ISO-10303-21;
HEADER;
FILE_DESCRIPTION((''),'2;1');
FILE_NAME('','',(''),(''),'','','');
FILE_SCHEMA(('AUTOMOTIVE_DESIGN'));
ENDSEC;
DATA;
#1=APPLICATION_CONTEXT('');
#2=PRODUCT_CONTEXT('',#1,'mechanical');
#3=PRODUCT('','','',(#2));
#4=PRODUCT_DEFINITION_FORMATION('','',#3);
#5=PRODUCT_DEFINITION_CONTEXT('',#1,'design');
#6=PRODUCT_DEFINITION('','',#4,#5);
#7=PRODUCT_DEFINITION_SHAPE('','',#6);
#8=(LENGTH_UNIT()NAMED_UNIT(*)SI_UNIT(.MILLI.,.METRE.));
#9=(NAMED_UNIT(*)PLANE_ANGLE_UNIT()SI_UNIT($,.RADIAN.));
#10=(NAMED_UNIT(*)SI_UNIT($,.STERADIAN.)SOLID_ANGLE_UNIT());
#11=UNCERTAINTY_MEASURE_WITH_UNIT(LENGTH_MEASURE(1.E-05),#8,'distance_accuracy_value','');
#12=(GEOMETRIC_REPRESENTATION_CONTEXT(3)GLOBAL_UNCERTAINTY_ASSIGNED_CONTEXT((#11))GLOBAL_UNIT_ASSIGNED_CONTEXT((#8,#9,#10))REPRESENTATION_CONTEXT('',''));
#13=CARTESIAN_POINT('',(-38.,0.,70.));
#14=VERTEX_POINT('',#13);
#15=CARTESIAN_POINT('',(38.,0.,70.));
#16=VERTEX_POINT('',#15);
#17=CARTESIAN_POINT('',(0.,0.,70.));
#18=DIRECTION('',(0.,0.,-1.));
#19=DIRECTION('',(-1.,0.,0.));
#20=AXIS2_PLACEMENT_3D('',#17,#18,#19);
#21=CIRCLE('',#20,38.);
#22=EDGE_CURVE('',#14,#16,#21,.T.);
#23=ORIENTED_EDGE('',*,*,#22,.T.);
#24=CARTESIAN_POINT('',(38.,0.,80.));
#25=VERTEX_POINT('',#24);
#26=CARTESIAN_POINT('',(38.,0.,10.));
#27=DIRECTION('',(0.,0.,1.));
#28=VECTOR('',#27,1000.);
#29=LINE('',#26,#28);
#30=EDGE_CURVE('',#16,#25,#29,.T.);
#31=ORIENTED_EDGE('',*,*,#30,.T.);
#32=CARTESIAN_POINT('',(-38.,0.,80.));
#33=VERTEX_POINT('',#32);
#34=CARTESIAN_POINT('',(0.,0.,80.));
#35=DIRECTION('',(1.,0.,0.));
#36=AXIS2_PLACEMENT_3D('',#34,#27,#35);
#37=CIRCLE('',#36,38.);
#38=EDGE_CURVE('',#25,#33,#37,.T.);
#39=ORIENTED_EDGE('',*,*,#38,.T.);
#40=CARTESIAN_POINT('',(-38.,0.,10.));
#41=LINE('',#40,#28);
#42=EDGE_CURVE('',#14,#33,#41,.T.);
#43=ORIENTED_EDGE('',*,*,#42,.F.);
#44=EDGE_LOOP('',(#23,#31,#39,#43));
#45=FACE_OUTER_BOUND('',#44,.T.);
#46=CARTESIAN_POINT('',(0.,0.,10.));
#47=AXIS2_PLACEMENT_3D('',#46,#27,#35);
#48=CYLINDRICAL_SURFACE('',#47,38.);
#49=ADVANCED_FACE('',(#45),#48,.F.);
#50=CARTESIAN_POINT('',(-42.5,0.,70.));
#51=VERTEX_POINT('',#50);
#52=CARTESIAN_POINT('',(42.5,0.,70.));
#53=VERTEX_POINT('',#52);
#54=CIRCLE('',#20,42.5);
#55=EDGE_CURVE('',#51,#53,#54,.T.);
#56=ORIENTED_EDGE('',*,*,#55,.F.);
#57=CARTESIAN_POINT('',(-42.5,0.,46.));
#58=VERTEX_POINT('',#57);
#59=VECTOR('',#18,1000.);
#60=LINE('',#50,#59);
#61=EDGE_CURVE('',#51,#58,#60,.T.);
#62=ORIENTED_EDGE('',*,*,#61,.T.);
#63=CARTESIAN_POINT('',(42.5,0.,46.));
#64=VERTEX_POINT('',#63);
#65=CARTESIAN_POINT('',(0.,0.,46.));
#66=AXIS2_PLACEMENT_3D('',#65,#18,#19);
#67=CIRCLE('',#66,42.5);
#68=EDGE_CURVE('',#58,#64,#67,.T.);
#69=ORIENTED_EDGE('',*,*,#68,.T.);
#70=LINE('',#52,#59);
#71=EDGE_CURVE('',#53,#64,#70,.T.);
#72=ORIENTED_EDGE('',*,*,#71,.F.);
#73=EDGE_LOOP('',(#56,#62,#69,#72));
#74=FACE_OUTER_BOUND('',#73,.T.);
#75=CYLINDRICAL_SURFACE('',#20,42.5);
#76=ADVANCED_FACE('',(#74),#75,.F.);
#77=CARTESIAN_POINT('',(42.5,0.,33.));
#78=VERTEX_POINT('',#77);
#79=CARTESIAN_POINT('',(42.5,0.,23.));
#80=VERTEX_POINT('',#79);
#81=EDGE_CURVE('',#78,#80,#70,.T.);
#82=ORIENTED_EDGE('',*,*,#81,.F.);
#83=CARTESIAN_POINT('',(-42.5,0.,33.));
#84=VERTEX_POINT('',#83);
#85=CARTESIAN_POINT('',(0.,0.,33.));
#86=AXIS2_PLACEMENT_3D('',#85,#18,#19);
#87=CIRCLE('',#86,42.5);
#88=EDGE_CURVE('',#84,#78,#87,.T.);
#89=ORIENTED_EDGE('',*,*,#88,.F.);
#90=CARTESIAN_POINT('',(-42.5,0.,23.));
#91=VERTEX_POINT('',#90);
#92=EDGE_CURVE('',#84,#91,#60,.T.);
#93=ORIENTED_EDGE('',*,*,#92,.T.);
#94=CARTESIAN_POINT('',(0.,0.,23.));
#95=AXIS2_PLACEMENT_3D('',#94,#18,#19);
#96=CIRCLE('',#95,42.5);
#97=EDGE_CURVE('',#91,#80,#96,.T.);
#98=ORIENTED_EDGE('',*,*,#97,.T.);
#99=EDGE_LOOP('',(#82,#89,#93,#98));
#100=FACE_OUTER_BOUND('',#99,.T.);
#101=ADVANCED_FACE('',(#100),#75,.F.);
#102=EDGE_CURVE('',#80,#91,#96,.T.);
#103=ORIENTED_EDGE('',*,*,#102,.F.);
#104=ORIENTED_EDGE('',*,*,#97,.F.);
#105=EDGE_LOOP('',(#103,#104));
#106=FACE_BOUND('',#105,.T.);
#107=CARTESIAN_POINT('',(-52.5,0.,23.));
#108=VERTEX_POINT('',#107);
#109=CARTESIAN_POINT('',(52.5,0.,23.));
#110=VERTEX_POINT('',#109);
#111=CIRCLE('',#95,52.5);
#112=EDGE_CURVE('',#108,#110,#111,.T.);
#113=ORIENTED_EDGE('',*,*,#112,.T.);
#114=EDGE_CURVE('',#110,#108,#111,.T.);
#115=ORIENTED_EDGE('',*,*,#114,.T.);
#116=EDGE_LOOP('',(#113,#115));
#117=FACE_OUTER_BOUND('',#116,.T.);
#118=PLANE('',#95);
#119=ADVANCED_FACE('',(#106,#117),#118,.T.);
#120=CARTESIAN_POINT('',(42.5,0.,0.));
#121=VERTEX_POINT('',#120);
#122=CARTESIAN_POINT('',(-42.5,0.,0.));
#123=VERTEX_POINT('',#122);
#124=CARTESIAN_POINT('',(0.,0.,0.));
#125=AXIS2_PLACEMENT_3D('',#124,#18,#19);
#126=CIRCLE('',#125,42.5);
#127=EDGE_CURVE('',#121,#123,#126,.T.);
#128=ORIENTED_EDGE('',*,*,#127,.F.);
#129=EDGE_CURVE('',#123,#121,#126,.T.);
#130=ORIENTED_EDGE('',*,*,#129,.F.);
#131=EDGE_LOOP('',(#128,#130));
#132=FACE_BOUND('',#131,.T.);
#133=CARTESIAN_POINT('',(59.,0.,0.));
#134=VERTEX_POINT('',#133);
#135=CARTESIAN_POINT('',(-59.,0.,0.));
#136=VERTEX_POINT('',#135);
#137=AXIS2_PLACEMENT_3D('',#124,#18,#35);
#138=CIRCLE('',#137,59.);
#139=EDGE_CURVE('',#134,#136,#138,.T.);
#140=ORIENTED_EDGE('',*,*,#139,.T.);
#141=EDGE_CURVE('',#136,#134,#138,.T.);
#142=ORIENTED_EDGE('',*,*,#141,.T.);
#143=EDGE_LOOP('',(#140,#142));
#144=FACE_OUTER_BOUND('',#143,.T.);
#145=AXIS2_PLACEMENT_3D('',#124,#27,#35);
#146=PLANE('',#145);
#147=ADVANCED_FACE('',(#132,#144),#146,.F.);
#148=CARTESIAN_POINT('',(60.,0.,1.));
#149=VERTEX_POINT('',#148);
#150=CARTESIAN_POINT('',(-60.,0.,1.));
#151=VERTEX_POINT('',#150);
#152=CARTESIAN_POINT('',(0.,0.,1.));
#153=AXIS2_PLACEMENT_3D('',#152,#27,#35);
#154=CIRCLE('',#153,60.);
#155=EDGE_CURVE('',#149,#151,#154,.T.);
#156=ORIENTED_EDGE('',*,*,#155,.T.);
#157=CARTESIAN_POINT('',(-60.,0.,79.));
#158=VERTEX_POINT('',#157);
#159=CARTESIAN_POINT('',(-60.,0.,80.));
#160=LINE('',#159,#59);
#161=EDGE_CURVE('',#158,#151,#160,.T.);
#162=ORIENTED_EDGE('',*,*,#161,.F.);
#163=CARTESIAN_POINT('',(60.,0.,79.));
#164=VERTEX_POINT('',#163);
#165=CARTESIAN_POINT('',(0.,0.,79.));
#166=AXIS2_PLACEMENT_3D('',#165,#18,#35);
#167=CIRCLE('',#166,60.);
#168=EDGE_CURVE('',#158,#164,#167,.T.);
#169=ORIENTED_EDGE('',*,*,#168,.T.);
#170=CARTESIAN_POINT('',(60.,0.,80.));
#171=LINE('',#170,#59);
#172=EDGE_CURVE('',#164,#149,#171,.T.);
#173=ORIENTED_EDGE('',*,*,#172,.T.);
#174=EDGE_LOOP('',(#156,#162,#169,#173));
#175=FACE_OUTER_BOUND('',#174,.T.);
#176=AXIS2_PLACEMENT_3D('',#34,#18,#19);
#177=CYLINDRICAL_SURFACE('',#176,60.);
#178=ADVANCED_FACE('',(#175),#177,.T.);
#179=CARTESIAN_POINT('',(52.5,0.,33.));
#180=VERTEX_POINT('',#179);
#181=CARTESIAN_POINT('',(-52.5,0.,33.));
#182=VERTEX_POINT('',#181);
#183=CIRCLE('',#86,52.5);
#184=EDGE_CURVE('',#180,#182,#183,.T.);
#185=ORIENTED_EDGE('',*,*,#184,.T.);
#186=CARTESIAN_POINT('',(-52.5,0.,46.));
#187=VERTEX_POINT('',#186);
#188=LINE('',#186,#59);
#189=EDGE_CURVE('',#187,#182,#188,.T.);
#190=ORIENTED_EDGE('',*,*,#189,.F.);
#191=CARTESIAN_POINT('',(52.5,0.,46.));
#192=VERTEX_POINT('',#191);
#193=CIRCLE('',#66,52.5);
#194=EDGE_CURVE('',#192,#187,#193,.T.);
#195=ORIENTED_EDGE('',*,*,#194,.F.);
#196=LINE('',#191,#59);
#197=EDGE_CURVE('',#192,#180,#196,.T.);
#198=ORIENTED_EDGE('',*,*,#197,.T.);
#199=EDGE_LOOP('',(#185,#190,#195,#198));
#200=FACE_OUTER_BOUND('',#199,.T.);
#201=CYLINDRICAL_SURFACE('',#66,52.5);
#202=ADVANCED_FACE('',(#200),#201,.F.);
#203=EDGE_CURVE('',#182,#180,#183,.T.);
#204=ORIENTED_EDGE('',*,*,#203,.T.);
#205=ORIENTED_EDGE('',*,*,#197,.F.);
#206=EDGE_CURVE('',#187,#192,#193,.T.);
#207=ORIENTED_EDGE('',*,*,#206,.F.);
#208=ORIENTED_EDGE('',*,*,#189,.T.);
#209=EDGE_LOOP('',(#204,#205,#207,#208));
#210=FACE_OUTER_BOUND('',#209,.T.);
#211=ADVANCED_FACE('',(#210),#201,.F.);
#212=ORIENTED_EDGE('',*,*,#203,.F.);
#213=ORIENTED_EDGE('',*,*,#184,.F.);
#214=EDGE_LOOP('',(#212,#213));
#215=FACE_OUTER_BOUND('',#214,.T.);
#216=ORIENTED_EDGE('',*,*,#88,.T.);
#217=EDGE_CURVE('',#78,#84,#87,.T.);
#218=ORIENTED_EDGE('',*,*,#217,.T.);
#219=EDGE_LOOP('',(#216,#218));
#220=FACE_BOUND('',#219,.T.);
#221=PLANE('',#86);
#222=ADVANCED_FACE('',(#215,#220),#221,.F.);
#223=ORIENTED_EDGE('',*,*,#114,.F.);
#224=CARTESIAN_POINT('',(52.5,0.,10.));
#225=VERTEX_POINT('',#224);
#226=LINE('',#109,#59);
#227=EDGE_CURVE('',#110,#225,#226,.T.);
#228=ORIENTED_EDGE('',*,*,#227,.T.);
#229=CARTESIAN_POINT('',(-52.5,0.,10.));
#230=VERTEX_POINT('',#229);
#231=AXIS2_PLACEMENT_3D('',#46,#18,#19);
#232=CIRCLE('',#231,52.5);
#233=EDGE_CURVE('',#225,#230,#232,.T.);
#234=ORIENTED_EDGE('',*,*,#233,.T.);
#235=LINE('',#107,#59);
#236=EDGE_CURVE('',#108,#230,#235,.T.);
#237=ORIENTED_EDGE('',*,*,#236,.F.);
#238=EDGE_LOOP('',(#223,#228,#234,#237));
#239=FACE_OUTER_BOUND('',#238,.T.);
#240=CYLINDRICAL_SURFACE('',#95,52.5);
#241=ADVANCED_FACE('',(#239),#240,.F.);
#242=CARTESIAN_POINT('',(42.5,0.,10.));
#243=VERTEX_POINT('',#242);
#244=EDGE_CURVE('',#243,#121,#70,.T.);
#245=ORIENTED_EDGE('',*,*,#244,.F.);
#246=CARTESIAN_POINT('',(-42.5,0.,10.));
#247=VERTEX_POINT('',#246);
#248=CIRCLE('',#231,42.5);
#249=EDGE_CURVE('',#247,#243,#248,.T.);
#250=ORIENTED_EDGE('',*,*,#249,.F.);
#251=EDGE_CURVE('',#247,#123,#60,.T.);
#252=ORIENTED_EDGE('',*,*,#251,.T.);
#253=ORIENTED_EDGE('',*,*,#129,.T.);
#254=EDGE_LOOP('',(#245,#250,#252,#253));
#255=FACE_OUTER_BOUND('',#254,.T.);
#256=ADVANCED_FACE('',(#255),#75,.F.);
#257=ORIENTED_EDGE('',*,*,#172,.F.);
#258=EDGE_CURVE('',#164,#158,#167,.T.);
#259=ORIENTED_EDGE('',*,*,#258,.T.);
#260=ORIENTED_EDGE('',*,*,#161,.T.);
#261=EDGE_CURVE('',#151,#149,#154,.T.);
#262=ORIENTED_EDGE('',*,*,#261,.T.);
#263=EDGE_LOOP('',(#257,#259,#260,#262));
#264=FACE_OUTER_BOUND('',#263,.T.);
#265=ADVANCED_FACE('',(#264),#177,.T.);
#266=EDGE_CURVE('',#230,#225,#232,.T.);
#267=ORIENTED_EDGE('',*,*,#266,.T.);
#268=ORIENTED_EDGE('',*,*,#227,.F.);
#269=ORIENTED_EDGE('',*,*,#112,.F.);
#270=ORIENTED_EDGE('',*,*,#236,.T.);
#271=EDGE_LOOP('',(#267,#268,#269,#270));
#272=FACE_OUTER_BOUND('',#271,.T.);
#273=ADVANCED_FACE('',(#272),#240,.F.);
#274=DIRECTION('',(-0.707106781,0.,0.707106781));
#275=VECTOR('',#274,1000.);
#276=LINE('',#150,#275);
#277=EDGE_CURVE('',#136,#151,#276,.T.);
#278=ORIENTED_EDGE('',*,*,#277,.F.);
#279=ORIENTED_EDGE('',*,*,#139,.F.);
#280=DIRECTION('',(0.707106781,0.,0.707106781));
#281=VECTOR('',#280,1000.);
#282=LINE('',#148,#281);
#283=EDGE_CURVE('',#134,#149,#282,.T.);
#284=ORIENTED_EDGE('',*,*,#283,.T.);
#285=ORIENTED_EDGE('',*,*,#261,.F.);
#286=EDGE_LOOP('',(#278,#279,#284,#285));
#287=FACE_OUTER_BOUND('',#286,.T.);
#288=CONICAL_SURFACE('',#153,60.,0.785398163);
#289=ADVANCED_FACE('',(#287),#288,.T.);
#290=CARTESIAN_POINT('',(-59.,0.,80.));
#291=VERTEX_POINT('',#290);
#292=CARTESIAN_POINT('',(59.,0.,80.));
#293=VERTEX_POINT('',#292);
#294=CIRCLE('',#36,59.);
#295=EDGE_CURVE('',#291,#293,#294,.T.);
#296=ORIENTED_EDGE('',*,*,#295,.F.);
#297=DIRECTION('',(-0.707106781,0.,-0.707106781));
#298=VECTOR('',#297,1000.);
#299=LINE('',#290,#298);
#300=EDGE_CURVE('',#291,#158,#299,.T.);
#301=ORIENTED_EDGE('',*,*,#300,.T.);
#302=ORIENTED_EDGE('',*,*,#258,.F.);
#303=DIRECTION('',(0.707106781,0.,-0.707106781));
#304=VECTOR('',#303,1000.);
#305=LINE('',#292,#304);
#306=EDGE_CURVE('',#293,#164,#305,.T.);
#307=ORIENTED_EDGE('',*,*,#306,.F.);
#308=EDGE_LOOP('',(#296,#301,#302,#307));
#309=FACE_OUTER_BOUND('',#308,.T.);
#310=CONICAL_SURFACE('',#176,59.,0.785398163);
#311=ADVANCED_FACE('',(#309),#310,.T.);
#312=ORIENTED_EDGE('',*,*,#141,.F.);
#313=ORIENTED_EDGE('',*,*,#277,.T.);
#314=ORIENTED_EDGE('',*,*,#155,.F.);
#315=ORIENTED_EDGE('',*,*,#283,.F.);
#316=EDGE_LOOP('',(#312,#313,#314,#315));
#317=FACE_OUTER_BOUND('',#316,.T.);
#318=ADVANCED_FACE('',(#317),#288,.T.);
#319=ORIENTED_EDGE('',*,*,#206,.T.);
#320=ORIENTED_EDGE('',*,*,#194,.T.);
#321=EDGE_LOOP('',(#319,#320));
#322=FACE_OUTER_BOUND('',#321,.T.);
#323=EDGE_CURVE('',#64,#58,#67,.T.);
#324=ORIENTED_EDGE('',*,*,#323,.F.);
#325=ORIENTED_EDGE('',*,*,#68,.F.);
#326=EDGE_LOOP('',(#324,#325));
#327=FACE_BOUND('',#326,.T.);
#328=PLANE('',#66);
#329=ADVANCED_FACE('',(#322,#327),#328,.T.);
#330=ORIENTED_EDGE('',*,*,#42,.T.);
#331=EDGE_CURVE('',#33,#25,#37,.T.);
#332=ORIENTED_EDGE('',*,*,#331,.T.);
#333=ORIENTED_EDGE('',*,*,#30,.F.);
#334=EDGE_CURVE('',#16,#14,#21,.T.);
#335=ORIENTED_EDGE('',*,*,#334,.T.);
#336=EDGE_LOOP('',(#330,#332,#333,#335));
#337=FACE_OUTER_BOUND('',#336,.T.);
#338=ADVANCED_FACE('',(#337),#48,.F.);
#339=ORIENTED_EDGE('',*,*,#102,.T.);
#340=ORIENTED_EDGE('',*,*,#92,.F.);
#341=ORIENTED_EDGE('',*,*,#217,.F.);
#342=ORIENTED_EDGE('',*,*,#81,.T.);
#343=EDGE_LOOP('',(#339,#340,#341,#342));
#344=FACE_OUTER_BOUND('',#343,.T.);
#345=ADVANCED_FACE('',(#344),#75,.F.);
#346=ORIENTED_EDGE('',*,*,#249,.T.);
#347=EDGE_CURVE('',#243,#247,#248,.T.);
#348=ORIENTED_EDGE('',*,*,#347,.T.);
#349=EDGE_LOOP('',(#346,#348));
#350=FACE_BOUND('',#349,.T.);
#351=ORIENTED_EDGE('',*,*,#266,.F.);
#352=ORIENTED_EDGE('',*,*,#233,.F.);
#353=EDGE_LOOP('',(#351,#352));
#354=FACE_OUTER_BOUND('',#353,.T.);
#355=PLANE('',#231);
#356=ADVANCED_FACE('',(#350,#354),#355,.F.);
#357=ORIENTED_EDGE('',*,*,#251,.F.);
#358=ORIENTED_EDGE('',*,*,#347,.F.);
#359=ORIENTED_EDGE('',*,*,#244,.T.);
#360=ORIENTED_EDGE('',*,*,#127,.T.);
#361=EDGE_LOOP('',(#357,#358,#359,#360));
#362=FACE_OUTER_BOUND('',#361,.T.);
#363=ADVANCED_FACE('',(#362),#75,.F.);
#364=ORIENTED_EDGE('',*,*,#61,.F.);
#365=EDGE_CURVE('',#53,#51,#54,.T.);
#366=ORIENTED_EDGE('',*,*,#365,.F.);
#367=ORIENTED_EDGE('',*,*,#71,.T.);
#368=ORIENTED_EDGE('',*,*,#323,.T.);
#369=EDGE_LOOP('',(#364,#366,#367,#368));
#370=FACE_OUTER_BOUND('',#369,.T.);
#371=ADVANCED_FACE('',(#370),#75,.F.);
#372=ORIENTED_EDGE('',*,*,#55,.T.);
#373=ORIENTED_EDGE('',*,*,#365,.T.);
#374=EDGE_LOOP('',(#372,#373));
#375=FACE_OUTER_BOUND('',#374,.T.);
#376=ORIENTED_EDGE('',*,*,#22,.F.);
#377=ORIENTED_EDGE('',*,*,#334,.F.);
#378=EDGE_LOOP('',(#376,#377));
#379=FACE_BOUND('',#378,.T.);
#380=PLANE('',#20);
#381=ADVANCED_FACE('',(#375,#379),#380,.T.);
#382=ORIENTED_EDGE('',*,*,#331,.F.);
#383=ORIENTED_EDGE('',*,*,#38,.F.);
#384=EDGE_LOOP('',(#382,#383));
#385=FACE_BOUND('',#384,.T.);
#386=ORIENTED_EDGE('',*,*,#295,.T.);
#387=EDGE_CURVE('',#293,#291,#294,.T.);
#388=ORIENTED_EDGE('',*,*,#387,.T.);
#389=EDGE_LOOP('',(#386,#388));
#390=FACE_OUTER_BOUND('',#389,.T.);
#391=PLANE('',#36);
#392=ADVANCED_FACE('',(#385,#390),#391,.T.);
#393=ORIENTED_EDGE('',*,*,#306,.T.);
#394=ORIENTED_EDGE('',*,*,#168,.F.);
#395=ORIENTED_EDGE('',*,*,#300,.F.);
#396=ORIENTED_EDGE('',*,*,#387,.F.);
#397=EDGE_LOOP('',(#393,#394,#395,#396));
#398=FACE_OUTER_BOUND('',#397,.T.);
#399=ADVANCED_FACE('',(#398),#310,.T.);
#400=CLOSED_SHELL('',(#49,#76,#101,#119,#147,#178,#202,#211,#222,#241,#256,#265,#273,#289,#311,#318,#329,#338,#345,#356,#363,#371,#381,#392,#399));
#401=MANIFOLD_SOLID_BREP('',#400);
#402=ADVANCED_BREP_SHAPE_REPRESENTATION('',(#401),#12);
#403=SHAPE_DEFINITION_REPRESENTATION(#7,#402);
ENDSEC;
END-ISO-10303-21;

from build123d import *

# Parameters (mm, degrees)
SKETCH_1_R          = 60
EXTRUDE_1_DEPTH     = 80
SKETCH_2_R          = 42.5
CUT_EXTRUDE_1_DEPTH = 70
SKETCH_3_R          = 38
CUT_EXTRUDE_2_DEPTH = 70
CHAMFER_1_SIZE      = 1
SKETCH_4_R          = 52.5
SKETCH_4_R_2        = 42.5
CUT_EXTRUDE_3_DEPTH = 13
SKETCH_5_R          = 52.5
SKETCH_5_R_2        = 42.5
CUT_EXTRUDE_4_DEPTH = 13


with BuildPart() as part:
    # 草图1 → 凸台-拉伸1 (new body)
    with BuildSketch(Plane.XY):
        Circle(SKETCH_1_R)
    extrude(amount=EXTRUDE_1_DEPTH)

    # 草图2 → 切除-拉伸1 (cut)
    with BuildSketch(Plane(origin=(0, 0, 0), x_dir=(-1, 0, 0), z_dir=(0, 0, -1))):
        Circle(SKETCH_2_R)
    extrude(amount=-CUT_EXTRUDE_1_DEPTH, mode=Mode.SUBTRACT)

    # 草图3 → 切除-拉伸2 (cut)
    with BuildSketch(Plane.XY.offset(80)):
        Circle(SKETCH_3_R)
    extrude(amount=-CUT_EXTRUDE_2_DEPTH, mode=Mode.SUBTRACT)

    # 倒角1
    chamfer_1_edges = [part.edges().sort_by_distance(p)[0] for p in [
        (-60, 0, 0),
        (-60, 0, 80),
    ]]
    chamfer(chamfer_1_edges, length=CHAMFER_1_SIZE)

    # 草图4 → 切除-拉伸3 (cut)
    with BuildSketch(Plane(origin=(0, 0, 10), x_dir=(-1, 0, 0), z_dir=(0, 0, -1))):
        Circle(SKETCH_4_R)
        Circle(SKETCH_4_R_2, mode=Mode.SUBTRACT)
    extrude(amount=-CUT_EXTRUDE_3_DEPTH, mode=Mode.SUBTRACT)

    # 草图5 → 切除-拉伸4 (cut)
    with BuildSketch(Plane(origin=(0, 0, 33), x_dir=(-1, 0, 0), z_dir=(0, 0, -1))):
        Circle(SKETCH_5_R)
        Circle(SKETCH_5_R_2, mode=Mode.SUBTRACT)
    extrude(amount=-CUT_EXTRUDE_4_DEPTH, mode=Mode.SUBTRACT)


solid = part.part
